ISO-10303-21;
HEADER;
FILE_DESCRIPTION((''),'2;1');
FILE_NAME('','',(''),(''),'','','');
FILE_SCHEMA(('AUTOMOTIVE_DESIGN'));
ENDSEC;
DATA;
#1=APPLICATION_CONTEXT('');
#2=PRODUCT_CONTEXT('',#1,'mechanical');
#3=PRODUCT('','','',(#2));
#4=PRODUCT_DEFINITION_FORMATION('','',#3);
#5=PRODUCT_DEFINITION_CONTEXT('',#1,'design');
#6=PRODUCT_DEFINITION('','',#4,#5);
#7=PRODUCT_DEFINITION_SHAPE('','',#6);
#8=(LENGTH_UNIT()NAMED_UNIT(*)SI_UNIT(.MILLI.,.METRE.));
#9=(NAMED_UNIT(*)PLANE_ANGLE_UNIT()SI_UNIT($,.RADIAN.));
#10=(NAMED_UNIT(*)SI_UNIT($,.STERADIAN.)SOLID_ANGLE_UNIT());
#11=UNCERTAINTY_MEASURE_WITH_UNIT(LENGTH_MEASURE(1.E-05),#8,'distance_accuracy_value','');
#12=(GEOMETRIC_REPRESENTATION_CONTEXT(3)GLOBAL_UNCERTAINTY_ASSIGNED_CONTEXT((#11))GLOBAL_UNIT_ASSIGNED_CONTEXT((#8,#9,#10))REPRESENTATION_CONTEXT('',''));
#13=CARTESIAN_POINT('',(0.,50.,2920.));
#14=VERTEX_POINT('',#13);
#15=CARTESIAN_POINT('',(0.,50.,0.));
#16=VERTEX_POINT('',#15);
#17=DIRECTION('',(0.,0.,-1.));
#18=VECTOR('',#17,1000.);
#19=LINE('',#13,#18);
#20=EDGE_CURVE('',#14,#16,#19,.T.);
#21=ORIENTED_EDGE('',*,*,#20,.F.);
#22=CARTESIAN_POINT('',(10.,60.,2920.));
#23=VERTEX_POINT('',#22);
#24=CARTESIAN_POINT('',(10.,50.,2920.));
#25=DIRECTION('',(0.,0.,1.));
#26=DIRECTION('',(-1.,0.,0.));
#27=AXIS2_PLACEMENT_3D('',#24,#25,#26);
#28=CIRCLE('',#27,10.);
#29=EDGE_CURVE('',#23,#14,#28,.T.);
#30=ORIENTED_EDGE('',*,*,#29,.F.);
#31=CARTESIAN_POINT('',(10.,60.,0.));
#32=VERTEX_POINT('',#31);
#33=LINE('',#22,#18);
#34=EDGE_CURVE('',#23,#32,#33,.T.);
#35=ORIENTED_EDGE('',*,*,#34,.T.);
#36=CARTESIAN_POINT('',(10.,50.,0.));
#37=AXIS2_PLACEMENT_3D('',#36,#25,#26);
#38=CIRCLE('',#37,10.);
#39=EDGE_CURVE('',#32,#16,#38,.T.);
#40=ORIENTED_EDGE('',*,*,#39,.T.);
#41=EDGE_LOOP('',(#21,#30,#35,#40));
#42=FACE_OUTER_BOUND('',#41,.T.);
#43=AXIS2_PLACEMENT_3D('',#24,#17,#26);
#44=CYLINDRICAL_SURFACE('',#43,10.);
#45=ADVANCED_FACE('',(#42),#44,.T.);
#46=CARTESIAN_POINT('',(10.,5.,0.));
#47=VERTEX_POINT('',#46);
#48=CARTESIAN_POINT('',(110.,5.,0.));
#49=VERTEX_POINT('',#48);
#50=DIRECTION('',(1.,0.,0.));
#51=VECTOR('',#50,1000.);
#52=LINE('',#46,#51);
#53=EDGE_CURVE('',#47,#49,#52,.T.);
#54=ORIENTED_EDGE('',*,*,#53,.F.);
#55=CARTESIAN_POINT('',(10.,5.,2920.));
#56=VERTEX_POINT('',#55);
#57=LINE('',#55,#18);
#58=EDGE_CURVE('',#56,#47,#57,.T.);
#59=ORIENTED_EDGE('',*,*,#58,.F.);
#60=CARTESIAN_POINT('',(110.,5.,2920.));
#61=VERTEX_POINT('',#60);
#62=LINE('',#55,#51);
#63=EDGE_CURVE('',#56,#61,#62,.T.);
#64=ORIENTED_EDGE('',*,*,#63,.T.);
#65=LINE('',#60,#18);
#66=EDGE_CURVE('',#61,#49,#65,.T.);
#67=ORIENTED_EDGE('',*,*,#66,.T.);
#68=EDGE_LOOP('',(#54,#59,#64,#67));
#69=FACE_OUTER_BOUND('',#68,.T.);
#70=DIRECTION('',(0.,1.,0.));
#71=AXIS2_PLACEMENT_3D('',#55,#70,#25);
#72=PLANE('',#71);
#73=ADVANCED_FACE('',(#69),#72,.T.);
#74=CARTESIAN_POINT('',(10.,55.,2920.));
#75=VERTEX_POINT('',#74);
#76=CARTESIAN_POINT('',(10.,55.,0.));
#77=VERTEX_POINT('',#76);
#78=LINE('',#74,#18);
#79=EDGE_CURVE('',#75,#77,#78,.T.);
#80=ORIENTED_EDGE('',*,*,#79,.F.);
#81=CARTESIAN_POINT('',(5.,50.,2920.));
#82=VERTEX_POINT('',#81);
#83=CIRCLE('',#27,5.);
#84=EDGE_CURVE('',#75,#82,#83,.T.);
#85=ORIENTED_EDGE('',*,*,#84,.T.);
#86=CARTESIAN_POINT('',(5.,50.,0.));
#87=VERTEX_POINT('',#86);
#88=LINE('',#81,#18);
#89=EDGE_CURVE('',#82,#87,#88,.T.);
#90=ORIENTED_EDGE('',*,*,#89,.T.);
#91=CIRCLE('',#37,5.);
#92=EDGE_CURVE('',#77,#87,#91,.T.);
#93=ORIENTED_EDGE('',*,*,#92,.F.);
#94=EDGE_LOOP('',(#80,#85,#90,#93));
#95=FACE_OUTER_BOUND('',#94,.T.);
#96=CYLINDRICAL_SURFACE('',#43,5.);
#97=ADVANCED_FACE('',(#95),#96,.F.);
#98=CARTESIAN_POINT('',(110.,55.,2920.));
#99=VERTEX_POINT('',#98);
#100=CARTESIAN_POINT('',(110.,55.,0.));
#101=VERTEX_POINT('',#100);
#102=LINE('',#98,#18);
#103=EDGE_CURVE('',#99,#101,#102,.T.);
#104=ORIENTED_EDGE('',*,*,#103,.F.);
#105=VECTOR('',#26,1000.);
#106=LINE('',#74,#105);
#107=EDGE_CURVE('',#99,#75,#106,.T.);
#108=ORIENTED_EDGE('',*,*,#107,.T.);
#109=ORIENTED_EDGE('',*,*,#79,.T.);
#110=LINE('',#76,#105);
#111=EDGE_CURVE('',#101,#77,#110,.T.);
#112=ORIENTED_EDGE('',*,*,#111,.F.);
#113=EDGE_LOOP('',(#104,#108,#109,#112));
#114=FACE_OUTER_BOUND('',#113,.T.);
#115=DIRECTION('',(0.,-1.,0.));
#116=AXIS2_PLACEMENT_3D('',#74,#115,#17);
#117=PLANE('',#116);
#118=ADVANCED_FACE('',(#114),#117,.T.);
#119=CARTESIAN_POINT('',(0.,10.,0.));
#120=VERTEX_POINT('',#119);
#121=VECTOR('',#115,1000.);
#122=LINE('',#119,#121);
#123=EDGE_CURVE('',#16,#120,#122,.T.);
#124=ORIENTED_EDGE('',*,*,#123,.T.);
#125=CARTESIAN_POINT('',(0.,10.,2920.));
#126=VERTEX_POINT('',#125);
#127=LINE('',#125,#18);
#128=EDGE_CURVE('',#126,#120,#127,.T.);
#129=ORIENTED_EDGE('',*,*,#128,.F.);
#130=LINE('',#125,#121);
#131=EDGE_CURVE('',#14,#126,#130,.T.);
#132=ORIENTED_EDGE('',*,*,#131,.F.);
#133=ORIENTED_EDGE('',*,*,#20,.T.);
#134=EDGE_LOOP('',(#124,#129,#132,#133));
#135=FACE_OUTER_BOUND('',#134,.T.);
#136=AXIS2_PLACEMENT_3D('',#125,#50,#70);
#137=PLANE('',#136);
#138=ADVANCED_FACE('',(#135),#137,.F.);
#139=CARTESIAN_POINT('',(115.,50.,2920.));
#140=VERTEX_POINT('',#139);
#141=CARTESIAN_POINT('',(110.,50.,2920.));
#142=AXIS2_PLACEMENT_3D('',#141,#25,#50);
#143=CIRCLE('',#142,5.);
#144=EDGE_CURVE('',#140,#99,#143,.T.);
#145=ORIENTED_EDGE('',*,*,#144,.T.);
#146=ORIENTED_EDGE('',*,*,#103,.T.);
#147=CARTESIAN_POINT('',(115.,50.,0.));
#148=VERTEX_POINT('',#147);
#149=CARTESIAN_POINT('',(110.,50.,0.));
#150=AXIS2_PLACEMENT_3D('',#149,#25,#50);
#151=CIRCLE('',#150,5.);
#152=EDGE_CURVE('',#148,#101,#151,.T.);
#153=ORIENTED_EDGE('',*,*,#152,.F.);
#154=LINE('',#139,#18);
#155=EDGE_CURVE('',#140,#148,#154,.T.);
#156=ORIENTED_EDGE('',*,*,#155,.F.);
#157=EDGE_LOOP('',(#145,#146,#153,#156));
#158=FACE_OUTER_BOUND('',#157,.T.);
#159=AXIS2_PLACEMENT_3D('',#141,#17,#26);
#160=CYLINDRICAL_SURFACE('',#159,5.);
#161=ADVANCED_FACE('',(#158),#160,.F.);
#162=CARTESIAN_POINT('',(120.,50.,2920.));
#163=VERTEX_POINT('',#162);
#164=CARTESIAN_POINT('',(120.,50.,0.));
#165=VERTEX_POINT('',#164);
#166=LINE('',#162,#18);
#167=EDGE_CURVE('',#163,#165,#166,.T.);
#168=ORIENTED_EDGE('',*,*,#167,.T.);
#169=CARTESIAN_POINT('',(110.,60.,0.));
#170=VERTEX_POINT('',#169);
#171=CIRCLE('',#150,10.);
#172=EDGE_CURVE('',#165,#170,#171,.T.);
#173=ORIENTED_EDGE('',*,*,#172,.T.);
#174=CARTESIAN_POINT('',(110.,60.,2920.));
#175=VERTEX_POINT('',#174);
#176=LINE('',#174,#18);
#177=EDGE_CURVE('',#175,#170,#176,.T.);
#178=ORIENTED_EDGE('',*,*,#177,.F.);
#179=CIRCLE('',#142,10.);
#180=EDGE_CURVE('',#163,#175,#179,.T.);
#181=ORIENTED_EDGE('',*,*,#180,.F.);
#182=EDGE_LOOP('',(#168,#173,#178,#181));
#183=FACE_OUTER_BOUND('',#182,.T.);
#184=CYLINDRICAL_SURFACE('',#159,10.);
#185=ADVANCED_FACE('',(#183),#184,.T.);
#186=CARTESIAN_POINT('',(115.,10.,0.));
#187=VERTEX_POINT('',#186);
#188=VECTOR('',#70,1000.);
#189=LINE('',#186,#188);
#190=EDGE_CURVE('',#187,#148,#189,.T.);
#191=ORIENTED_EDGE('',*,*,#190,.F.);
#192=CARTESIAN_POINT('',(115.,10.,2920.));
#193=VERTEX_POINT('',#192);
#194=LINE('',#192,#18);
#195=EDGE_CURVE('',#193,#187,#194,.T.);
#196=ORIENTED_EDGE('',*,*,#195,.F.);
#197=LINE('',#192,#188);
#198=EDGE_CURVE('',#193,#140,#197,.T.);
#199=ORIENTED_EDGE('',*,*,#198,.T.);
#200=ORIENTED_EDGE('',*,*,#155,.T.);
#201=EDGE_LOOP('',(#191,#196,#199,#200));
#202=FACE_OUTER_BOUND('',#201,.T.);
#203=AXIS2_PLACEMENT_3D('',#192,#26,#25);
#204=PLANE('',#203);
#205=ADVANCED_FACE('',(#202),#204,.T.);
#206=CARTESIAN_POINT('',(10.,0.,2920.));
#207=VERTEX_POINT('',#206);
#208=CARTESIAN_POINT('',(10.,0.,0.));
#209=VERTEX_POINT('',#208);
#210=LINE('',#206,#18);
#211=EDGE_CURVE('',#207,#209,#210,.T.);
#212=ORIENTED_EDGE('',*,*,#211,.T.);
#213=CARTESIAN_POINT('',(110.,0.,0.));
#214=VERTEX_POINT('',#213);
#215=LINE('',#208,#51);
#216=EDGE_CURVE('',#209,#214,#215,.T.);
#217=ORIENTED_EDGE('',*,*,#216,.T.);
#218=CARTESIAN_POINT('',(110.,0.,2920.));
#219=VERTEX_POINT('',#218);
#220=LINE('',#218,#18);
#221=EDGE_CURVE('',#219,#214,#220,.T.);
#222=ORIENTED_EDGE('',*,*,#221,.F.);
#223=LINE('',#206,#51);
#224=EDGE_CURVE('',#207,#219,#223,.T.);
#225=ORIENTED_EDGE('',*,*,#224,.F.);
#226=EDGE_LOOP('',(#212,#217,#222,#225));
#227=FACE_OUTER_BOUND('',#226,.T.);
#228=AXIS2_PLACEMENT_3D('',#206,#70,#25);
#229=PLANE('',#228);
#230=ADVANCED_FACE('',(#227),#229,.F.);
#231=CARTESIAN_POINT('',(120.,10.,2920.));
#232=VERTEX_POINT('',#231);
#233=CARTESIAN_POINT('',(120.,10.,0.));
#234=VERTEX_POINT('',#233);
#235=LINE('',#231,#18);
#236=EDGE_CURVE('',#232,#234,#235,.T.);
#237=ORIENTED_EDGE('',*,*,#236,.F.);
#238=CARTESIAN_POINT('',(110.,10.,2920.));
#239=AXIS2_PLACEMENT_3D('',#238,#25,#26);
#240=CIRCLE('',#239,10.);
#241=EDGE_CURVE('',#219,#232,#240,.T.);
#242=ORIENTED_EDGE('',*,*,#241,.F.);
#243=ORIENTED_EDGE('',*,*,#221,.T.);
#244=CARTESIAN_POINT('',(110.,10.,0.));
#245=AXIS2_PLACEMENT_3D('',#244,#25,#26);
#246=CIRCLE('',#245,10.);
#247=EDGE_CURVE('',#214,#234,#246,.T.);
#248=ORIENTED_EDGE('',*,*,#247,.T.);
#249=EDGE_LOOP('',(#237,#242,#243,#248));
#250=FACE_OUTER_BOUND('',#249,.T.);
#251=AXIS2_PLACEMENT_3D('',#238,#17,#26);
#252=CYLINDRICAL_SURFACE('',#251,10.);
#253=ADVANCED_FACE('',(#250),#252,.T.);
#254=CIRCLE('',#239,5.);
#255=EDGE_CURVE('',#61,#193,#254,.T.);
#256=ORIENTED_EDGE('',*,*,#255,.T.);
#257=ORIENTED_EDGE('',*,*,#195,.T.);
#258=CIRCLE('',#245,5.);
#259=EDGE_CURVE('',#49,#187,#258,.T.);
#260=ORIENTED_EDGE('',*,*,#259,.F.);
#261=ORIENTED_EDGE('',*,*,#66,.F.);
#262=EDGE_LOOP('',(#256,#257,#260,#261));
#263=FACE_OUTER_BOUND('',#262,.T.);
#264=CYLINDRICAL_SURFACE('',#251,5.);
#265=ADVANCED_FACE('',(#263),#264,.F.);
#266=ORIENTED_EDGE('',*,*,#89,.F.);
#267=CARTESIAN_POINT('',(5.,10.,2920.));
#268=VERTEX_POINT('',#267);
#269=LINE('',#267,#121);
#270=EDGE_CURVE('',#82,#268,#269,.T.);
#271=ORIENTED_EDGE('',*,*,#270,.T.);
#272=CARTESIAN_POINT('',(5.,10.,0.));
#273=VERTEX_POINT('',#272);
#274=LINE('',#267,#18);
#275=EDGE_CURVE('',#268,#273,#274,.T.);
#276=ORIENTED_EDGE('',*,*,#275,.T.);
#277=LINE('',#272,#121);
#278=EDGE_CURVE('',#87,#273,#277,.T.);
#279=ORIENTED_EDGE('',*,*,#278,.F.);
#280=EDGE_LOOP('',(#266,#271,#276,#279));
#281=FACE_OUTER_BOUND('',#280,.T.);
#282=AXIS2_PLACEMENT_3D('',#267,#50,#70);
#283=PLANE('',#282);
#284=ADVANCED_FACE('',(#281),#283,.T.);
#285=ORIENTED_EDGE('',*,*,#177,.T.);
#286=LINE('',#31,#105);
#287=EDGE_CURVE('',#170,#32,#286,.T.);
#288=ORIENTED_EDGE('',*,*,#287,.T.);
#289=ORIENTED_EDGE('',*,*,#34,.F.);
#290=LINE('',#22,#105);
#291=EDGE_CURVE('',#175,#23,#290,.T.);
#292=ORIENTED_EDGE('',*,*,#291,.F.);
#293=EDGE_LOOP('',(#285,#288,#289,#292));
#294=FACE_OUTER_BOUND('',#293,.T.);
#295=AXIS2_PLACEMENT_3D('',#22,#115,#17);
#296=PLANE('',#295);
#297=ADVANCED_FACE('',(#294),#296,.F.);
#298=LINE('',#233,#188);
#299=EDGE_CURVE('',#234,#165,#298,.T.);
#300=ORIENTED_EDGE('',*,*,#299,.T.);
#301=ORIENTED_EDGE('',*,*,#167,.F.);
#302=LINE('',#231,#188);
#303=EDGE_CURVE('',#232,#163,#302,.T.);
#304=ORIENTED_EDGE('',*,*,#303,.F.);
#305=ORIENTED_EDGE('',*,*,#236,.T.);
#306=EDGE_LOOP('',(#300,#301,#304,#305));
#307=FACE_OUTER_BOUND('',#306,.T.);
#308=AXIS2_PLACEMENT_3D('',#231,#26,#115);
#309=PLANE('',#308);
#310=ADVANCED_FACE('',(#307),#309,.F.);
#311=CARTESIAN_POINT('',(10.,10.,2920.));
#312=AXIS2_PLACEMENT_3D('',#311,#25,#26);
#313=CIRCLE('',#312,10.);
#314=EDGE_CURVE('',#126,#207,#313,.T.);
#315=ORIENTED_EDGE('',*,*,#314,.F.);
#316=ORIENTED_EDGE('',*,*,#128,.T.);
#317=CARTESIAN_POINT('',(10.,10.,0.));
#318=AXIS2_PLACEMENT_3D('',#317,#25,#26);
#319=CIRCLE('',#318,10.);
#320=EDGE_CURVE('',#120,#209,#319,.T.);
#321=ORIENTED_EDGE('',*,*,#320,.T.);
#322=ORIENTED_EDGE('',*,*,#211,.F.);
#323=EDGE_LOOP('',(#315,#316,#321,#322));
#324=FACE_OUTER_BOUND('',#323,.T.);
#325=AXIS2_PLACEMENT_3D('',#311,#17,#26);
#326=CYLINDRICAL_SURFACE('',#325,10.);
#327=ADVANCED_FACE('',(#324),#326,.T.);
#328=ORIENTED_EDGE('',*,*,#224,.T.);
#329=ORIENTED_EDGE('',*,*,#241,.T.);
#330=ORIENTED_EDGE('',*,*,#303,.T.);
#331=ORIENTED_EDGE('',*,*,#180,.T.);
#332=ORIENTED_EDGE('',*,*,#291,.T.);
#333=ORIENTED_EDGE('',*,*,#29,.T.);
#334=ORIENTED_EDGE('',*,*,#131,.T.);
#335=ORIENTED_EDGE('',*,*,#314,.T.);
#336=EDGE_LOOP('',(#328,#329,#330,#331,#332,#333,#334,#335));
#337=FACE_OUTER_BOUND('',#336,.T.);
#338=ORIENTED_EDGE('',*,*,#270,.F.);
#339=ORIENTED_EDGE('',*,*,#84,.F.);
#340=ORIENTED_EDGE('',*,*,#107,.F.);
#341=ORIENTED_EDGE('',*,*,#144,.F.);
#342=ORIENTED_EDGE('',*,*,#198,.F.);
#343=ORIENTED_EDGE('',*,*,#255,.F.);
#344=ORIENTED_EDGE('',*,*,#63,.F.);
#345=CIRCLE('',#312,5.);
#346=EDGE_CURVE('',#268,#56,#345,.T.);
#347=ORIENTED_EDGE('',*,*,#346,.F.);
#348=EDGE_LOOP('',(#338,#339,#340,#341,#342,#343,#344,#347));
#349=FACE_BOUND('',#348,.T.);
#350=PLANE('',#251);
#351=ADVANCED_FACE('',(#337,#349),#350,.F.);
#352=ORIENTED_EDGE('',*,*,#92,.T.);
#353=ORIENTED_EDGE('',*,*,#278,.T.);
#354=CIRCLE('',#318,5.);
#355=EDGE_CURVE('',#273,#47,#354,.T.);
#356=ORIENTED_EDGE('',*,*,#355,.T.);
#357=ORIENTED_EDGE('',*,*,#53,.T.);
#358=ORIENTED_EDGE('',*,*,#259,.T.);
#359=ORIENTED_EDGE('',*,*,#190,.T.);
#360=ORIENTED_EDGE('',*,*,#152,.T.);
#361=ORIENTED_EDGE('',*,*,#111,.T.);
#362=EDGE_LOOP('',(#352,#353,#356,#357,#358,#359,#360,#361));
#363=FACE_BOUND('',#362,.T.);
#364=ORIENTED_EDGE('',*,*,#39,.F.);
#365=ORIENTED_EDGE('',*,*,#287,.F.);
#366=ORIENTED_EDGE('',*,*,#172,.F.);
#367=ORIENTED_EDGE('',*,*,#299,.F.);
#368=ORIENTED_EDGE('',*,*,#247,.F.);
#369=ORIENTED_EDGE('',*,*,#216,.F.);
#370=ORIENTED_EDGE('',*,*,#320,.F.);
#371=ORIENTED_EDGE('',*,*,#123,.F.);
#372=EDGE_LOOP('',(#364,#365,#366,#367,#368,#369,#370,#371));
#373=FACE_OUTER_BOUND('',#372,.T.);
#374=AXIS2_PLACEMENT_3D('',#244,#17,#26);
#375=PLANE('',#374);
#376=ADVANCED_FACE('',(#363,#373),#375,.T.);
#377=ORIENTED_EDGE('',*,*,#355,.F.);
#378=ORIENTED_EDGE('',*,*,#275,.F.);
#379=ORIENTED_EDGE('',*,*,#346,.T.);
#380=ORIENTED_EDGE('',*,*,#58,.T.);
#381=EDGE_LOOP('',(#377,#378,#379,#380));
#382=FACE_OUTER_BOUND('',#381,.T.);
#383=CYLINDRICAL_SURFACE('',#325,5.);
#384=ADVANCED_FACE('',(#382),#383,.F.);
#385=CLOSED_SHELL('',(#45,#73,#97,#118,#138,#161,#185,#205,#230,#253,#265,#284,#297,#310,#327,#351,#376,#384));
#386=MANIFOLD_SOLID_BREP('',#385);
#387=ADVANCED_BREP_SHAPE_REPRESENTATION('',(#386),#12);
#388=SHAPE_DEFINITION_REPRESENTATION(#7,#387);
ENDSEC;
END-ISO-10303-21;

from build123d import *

# Parameters (mm, degrees)
BOSS_EXTRUDE1_DEPTH = 2920


with BuildPart() as part:
    # Sketch1 → Boss-Extrude1 (new body)
    with BuildSketch(Plane.XY):
        with BuildLine():
            Line((10, 0), (110, 0))
            ThreePointArc((110, 0), (117.071067812, 2.928932188), (120, 10))
            Line((120, 10), (120, 50))
            ThreePointArc((120, 50), (117.071067812, 57.071067812), (110, 60))
            Line((110, 60), (10, 60))
            ThreePointArc((10, 60), (2.928932188, 57.071067812), (0, 50))
            Line((0, 50), (0, 10))
            ThreePointArc((0, 10), (2.928932188, 2.928932188), (10, 0))
        make_face()
        with BuildLine():
            Line((10, 55), (110, 55))
            ThreePointArc((110, 55), (113.535533906, 53.535533906), (115, 50))
            Line((115, 50), (115, 10))
            ThreePointArc((115, 10), (113.535533906, 6.464466094), (110, 5))
            Line((110, 5), (10, 5))
            ThreePointArc((10, 5), (6.464466094, 6.464466094), (5, 10))
            Line((5, 10), (5, 50))
            ThreePointArc((5, 50), (6.464466094, 53.535533906), (10, 55))
        make_face(mode=Mode.SUBTRACT)
    extrude(amount=BOSS_EXTRUDE1_DEPTH)


solid = part.part
